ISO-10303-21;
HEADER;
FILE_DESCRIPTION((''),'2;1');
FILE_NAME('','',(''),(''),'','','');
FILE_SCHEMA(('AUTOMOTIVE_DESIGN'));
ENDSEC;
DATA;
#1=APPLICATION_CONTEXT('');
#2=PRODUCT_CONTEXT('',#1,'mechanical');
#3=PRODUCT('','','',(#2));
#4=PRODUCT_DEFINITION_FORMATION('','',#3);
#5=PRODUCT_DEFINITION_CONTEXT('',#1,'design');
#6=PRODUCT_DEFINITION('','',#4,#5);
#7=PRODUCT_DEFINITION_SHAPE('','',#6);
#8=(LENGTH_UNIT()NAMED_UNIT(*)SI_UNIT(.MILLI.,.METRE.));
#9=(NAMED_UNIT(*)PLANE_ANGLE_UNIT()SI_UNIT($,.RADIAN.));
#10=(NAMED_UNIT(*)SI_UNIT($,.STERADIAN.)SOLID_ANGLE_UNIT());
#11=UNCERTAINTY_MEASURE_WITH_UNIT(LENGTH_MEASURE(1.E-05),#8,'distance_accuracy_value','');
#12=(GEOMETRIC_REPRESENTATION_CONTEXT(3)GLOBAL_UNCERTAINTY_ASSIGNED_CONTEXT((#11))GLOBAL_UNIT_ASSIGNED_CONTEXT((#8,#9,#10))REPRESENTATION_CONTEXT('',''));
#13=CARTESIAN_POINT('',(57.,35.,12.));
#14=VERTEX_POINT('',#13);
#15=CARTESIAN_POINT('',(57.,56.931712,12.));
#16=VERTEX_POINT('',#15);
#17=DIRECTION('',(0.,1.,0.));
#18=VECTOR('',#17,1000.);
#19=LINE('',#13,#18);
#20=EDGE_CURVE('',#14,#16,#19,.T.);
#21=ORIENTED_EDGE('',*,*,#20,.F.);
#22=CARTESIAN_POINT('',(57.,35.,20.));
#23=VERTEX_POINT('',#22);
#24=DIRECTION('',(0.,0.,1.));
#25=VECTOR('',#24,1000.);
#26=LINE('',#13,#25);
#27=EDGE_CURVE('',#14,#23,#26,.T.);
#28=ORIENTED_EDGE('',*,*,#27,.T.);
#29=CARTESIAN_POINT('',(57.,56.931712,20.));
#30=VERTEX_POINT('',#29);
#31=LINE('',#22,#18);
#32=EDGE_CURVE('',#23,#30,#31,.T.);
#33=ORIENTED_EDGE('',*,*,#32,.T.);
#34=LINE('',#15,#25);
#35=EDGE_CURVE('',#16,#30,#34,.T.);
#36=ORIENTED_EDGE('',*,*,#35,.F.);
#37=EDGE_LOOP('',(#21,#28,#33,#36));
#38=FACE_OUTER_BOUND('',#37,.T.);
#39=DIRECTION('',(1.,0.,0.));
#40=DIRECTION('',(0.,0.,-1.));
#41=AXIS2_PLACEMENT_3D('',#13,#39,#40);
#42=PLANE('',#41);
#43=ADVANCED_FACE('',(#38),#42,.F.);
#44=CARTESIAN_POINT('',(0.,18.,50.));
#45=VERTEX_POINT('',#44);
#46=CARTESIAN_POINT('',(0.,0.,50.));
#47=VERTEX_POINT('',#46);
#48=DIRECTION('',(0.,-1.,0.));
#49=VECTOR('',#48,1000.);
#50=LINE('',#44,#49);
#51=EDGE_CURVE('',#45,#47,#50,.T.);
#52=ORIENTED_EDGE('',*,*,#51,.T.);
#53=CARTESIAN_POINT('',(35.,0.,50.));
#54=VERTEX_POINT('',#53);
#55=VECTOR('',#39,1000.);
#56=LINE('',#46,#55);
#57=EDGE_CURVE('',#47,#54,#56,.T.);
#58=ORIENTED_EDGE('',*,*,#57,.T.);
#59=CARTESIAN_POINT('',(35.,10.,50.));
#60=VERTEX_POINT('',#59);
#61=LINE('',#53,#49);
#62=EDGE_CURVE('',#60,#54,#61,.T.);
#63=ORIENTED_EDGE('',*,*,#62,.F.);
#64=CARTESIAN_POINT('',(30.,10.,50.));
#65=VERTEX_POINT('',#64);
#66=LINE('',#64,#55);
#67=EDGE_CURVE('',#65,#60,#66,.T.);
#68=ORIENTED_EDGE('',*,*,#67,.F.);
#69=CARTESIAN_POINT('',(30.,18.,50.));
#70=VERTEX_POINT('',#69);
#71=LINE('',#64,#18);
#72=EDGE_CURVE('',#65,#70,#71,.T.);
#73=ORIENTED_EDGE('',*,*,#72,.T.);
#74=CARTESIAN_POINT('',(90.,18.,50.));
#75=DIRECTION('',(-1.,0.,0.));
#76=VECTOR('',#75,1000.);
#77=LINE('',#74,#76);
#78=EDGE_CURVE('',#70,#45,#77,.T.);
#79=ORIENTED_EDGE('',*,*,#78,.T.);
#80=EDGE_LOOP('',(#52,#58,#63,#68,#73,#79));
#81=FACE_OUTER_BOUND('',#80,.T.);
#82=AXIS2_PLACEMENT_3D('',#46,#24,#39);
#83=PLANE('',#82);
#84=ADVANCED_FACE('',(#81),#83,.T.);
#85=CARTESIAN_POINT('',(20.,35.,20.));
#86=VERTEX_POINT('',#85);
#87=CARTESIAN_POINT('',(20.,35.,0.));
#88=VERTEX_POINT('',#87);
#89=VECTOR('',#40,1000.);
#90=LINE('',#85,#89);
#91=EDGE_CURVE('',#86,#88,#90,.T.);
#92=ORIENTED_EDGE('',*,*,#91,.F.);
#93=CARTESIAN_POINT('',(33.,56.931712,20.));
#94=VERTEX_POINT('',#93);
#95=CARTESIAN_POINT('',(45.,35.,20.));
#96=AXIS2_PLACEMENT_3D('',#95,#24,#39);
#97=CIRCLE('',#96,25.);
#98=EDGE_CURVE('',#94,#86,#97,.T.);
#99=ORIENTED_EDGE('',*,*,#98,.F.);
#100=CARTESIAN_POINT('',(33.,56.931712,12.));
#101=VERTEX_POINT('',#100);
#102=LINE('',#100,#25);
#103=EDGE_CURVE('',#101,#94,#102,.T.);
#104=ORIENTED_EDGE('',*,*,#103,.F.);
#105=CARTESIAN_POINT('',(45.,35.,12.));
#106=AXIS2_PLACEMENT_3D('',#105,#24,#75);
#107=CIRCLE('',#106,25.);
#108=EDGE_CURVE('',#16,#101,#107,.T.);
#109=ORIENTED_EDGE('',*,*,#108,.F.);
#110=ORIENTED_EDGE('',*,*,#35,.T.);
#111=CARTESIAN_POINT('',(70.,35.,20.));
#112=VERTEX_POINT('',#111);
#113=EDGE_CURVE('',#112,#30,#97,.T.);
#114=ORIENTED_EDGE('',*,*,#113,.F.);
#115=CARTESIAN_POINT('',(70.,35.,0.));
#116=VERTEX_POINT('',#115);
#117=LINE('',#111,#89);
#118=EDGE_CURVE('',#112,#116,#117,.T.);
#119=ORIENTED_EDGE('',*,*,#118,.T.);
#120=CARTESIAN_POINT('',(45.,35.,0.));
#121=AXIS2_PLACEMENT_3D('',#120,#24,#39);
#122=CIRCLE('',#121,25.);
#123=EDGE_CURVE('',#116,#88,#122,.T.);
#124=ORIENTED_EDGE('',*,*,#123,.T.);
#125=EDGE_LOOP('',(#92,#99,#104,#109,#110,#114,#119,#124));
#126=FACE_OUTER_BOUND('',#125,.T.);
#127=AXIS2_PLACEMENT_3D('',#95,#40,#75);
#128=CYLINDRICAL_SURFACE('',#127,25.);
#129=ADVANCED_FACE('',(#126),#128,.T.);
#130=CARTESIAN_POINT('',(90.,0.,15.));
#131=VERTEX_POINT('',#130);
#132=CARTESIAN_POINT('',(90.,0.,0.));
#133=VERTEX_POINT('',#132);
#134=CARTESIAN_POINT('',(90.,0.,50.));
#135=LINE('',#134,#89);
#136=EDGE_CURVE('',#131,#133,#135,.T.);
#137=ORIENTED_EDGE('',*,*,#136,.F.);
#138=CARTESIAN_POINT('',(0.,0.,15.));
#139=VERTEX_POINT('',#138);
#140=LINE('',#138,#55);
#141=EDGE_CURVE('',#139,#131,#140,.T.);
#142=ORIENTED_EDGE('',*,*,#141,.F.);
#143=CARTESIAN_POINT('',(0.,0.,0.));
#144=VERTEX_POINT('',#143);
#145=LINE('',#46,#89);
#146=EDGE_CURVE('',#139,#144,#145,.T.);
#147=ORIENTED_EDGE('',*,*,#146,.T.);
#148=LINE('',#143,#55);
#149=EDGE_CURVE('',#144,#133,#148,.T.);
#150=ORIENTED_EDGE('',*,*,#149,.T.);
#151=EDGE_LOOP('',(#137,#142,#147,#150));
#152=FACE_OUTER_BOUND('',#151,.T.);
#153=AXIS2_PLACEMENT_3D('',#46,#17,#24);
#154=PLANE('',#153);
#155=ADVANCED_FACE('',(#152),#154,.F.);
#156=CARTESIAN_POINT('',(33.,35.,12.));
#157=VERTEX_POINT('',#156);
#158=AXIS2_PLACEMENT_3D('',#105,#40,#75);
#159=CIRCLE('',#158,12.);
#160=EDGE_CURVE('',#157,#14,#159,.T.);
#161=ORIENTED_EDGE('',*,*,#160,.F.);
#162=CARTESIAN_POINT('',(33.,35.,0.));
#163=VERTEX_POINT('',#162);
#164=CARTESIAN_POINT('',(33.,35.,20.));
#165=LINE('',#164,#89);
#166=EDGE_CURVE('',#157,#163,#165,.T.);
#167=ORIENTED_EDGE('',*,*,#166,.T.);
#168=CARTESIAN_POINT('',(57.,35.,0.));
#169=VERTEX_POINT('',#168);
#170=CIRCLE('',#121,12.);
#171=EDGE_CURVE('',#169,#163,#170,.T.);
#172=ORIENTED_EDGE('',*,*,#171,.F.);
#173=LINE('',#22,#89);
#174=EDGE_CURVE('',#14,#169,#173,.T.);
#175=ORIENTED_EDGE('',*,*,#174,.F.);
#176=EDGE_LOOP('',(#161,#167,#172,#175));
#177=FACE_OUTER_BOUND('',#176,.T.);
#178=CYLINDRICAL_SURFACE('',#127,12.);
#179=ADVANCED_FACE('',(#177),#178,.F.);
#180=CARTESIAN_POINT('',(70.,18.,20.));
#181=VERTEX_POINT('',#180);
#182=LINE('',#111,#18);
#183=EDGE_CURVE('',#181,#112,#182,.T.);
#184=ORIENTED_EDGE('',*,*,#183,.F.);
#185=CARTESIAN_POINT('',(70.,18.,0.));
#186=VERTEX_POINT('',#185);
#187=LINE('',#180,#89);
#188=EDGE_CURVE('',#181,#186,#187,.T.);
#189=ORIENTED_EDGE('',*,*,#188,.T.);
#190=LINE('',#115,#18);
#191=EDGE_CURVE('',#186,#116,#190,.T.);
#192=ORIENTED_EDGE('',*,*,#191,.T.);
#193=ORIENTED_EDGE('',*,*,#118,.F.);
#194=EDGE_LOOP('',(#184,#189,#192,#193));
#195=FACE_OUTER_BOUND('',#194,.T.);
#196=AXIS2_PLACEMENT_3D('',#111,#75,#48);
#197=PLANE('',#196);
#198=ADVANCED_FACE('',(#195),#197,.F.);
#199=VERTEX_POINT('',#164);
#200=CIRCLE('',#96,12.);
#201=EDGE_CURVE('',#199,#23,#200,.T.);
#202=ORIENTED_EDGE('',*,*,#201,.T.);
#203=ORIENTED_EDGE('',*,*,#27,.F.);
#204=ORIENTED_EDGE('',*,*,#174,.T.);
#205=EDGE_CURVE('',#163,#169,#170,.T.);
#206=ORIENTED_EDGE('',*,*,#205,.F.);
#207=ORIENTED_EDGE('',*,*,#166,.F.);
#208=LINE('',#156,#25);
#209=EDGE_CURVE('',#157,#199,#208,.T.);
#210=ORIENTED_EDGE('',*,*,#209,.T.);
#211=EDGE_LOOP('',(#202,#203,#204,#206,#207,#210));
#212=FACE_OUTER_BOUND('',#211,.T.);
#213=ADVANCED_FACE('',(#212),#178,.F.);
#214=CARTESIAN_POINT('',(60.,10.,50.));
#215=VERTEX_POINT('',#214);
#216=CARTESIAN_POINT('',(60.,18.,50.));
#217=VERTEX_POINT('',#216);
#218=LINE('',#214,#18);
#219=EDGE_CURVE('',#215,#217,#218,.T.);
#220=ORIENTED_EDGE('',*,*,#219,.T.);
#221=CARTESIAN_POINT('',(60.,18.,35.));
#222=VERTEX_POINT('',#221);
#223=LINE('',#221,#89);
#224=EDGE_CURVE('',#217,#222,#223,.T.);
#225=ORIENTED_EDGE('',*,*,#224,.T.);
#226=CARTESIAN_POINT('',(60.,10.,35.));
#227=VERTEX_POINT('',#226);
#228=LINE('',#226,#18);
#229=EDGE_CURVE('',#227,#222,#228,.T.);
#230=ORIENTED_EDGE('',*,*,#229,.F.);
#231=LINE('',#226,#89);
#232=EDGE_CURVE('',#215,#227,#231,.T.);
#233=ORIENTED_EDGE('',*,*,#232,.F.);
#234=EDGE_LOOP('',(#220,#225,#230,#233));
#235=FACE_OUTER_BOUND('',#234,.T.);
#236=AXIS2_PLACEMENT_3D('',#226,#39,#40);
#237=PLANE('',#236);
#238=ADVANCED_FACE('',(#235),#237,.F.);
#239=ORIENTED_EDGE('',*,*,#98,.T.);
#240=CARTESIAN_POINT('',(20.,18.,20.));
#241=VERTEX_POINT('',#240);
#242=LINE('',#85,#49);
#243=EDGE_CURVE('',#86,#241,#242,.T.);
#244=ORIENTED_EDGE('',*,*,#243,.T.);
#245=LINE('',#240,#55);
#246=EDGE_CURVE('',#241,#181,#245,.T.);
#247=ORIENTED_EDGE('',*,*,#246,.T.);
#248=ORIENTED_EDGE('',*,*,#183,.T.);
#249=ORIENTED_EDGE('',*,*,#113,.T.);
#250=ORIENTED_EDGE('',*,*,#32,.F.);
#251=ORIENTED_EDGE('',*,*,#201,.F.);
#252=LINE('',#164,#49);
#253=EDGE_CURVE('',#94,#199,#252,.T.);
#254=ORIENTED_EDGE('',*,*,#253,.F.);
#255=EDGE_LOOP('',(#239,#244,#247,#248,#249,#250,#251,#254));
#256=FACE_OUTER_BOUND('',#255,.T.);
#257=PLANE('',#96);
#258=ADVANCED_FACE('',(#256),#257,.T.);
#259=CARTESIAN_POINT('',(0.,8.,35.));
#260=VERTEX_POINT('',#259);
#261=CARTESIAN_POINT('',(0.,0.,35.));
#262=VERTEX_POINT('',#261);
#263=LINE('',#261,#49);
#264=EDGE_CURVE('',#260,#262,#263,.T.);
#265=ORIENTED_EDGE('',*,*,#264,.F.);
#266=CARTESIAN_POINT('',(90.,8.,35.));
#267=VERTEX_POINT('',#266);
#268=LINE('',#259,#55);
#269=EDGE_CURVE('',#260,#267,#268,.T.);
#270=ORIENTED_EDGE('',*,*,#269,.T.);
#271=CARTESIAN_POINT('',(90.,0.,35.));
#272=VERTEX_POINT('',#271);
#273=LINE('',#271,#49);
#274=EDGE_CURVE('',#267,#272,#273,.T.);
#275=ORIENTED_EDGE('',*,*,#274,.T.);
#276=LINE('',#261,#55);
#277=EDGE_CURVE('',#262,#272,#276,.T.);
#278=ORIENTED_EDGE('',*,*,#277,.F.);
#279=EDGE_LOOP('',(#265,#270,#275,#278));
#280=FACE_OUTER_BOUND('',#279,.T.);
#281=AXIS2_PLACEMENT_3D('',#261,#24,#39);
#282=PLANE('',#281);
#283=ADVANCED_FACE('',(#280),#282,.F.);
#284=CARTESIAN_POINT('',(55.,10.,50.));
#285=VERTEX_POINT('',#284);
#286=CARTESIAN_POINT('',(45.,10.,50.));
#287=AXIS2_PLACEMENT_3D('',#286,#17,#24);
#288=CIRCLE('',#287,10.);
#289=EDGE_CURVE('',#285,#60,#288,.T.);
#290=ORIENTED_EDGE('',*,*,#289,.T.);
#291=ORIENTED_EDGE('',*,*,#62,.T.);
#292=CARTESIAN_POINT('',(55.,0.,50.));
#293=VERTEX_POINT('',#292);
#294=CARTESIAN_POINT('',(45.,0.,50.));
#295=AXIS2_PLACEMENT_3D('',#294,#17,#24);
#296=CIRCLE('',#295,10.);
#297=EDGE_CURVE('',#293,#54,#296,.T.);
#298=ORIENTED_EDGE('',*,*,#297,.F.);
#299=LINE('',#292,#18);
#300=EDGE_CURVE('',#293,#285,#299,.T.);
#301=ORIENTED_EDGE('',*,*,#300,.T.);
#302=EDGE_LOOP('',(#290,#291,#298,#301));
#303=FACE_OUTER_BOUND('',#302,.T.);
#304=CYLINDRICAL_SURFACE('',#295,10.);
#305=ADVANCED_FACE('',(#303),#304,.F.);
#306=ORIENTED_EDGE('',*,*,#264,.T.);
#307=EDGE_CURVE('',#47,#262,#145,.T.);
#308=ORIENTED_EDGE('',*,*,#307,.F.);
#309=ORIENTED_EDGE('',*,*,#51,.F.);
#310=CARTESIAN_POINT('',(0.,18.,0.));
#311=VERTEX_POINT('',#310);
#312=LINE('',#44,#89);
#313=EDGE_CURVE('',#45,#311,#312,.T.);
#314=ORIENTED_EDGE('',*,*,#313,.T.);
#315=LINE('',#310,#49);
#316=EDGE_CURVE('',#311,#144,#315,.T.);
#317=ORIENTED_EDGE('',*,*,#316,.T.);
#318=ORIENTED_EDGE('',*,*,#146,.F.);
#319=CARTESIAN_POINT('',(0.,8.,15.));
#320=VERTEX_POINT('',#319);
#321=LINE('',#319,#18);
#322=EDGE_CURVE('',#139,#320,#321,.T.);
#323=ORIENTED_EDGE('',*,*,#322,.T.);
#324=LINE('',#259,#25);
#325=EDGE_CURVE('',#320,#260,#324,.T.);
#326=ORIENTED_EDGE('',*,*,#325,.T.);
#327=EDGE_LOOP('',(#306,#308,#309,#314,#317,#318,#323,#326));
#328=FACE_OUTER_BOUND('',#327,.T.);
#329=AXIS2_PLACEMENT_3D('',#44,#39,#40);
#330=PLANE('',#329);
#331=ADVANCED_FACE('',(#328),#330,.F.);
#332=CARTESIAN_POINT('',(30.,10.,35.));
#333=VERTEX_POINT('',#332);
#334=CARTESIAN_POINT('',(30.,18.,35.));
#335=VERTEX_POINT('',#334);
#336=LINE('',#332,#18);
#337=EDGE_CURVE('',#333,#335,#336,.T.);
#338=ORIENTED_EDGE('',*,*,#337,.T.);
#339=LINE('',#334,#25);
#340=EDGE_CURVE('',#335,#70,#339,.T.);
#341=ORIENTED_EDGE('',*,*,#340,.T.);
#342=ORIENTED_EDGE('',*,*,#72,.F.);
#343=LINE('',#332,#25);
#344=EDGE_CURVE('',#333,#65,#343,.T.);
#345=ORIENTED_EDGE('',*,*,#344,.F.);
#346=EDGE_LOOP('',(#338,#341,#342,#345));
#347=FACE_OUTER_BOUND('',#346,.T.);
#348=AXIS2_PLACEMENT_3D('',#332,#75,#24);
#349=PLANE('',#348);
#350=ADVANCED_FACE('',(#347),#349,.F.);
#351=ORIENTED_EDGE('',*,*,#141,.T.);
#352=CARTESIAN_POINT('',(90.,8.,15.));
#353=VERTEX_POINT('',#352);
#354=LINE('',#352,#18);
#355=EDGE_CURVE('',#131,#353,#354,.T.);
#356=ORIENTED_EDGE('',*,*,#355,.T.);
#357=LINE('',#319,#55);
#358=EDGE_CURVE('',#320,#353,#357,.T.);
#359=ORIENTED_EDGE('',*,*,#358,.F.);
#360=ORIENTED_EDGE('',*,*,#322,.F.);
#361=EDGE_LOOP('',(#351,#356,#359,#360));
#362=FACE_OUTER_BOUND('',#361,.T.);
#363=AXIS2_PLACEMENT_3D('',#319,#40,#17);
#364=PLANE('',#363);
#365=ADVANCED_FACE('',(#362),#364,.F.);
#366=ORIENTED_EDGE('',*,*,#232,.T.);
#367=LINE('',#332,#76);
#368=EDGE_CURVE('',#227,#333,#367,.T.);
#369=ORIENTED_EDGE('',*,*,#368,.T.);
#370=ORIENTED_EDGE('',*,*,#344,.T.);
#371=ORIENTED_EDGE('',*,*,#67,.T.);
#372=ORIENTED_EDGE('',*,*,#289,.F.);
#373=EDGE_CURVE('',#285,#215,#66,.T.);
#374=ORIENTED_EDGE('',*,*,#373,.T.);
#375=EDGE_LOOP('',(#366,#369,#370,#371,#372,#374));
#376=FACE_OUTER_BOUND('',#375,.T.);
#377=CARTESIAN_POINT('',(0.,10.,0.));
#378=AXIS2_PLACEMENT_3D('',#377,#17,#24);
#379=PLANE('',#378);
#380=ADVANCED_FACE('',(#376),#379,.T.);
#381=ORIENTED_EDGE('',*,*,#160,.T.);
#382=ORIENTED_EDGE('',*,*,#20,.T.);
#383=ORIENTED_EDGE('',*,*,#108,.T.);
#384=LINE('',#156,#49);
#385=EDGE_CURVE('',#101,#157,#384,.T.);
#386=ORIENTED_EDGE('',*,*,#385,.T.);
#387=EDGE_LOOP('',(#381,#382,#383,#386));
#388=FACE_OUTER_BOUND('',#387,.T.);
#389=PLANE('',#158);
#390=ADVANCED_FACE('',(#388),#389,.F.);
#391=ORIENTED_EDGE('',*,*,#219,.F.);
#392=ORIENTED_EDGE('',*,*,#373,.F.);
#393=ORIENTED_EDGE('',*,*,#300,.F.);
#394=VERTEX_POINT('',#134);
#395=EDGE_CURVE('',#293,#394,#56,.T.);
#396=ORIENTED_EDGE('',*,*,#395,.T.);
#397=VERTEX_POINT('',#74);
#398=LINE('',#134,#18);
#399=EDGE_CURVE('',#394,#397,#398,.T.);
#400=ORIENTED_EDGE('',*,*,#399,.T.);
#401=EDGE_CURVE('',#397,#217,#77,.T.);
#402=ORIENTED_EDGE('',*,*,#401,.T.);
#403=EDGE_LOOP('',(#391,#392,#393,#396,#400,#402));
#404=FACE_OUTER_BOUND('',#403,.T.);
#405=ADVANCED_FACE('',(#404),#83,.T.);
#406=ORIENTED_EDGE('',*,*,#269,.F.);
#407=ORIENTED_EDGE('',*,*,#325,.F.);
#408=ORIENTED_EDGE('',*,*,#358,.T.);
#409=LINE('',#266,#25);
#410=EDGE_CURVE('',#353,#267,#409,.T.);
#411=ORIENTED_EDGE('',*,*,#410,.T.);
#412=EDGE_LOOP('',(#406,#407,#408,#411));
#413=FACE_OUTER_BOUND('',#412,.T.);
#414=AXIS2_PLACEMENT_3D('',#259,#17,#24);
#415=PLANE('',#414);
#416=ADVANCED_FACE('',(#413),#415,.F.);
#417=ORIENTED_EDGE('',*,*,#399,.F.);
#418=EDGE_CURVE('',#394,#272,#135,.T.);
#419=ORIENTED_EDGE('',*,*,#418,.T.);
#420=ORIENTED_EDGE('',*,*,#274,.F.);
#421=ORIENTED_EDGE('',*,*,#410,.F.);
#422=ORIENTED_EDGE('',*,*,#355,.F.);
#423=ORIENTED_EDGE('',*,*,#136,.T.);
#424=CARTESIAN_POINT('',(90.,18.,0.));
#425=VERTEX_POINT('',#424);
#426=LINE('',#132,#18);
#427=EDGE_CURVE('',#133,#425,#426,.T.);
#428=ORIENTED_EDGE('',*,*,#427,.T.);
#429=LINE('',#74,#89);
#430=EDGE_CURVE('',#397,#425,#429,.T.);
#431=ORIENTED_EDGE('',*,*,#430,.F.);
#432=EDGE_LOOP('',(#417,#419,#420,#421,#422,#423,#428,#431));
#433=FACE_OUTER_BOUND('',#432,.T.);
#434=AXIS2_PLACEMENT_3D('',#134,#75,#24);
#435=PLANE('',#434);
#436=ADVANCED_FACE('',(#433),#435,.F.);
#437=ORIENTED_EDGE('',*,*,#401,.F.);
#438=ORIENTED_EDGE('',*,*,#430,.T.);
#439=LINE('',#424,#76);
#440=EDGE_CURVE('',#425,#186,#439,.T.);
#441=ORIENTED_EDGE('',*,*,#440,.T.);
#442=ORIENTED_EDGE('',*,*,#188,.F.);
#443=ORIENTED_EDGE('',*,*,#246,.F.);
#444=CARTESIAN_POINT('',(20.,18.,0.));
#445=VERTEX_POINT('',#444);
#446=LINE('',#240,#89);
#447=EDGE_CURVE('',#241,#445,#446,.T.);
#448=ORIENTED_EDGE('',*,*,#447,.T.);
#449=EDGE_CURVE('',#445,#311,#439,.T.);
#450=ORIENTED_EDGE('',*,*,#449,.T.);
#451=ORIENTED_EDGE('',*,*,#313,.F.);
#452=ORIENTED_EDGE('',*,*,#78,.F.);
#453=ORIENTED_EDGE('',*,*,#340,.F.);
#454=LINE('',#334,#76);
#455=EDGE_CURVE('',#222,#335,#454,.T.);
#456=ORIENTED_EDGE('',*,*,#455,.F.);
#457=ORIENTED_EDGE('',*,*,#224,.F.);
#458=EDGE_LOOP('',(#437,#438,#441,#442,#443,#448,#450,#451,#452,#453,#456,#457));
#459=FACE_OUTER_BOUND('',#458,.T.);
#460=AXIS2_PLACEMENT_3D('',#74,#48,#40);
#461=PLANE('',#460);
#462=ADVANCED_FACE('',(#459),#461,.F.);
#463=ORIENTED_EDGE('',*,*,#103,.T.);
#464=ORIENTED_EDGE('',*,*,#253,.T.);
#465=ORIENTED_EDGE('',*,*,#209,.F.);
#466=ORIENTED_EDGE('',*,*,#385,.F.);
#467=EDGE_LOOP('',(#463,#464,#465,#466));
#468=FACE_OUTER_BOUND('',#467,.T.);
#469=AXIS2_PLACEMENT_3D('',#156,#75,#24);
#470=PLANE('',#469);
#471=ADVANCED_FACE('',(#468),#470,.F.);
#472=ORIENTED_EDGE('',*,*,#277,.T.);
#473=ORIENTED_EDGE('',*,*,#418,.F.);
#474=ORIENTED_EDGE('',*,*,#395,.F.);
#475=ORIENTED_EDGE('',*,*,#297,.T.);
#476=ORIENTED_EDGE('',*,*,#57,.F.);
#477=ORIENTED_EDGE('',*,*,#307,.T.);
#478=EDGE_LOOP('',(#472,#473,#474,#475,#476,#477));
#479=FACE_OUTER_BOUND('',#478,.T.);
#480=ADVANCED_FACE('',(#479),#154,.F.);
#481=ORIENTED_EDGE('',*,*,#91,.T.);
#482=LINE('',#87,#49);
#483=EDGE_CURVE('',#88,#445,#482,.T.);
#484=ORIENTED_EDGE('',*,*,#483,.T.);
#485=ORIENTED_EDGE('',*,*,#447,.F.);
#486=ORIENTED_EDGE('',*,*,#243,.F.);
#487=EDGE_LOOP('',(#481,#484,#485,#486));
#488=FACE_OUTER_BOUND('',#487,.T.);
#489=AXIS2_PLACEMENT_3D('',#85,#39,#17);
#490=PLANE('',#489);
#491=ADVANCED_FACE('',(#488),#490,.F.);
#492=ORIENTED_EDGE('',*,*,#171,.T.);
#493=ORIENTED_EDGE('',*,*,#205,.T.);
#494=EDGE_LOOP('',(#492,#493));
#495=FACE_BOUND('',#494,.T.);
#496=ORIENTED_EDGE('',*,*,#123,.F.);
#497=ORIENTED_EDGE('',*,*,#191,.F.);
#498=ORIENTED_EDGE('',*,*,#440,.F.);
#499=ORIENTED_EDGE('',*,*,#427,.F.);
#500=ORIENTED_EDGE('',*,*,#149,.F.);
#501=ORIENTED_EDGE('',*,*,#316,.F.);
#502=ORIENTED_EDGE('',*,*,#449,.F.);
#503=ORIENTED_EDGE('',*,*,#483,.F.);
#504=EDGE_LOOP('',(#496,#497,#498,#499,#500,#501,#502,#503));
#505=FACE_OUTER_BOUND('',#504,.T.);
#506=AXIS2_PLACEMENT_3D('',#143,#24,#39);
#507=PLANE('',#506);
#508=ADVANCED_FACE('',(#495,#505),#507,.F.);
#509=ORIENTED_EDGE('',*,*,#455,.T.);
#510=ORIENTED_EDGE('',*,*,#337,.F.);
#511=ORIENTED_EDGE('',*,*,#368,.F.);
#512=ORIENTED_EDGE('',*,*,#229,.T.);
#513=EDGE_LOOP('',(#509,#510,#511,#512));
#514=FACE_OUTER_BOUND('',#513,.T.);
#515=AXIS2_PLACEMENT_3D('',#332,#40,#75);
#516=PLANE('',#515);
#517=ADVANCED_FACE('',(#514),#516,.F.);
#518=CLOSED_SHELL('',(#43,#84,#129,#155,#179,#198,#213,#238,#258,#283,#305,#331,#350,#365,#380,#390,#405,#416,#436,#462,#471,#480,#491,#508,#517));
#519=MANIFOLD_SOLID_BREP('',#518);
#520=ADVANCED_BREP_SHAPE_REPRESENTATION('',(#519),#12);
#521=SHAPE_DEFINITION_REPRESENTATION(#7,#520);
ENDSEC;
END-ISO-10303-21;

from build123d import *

# Parameters (mm, degrees)
BASE_PLATE_SKETCH_W       = 90
BASE_PLATE_SKETCH_H       = 18
BASE_PLATE_90X18X50_DEPTH = 50
PIVOT_LUG_SKETCH_R        = 12
PIVOT_LUG_DEPTH           = 20
BOTTOM_GROOVE_SKETCH_W    = 20
BOTTOM_GROOVE_SKETCH_H    = 8
BOTTOM_GROOVE_DEPTH       = 120.163752878
LUG_START                 = -8
LUG_SLOT_DEPTH            = 8
TOP_POCKET_SKETCH_W       = 30
TOP_POCKET_SKETCH_H       = 15
TOP_POCKET_DEPTH          = 8
POCKET_HOLE_20_SKETCH_R   = 10
POCKET_HOLE_20_DEPTH      = 115.455231423


with BuildPart() as part:
    # Base Plate Sketch → Base Plate 90x18x50 (new body)
    with BuildSketch(Plane.XY):
        with Locations((45, 9)):
            Rectangle(BASE_PLATE_SKETCH_W, BASE_PLATE_SKETCH_H)
    extrude(amount=BASE_PLATE_90X18X50_DEPTH)

    # Pivot Lug Sketch → Pivot Lug (add)
    with BuildSketch(Plane.XY):
        with BuildLine():
            Line((20, 35), (20, 18))
            Line((20, 18), (70, 18))
            Line((70, 18), (70, 35))
            ThreePointArc((70, 35), (45, 60), (20, 35))
        make_face()
        with Locations((45, 35)):
            Circle(PIVOT_LUG_SKETCH_R, mode=Mode.SUBTRACT)
    extrude(amount=PIVOT_LUG_DEPTH)

    # Bottom Groove Sketch → Bottom Groove (cut, through all)
    with BuildSketch(Plane(origin=(90, 0, 0), x_dir=(0, 0, -1), z_dir=(1, 0, 0))):
        with Locations((-25, 4)):
            Rectangle(BOTTOM_GROOVE_SKETCH_W, BOTTOM_GROOVE_SKETCH_H)
    extrude(amount=-BOTTOM_GROOVE_DEPTH, mode=Mode.SUBTRACT)

    # Lug Slot Sketch → Lug Slot (cut)
    with BuildSketch(Plane.XY.offset(20).offset(LUG_START)):
        with BuildLine():
            Line((33, 35), (33, 56.931712199))
            ThreePointArc((33, 56.931712199), (45, 60), (57, 56.931712199))
            Line((57, 56.931712199), (57, 35))
            ThreePointArc((57, 35), (45, 47), (33, 35))
        make_face()
    extrude(amount=LUG_SLOT_DEPTH, mode=Mode.SUBTRACT)

    # Top Pocket Sketch → Top Pocket (cut)
    with BuildSketch(Plane(origin=(0, 18, 0), x_dir=(1, 0, 0), z_dir=(0, 1, 0))):
        with Locations((45, -42.5)):
            Rectangle(TOP_POCKET_SKETCH_W, TOP_POCKET_SKETCH_H)
    extrude(amount=-TOP_POCKET_DEPTH, mode=Mode.SUBTRACT)

    # Pocket Hole Ø20 Sketch → Pocket Hole Ø20 (cut, through all)
    with BuildSketch(Plane(origin=(0, 10, 0), x_dir=(1, 0, 0), z_dir=(0, 1, 0))):
        with Locations((45, -50)):
            Circle(POCKET_HOLE_20_SKETCH_R)
    extrude(amount=-POCKET_HOLE_20_DEPTH, mode=Mode.SUBTRACT)


solid = part.part
